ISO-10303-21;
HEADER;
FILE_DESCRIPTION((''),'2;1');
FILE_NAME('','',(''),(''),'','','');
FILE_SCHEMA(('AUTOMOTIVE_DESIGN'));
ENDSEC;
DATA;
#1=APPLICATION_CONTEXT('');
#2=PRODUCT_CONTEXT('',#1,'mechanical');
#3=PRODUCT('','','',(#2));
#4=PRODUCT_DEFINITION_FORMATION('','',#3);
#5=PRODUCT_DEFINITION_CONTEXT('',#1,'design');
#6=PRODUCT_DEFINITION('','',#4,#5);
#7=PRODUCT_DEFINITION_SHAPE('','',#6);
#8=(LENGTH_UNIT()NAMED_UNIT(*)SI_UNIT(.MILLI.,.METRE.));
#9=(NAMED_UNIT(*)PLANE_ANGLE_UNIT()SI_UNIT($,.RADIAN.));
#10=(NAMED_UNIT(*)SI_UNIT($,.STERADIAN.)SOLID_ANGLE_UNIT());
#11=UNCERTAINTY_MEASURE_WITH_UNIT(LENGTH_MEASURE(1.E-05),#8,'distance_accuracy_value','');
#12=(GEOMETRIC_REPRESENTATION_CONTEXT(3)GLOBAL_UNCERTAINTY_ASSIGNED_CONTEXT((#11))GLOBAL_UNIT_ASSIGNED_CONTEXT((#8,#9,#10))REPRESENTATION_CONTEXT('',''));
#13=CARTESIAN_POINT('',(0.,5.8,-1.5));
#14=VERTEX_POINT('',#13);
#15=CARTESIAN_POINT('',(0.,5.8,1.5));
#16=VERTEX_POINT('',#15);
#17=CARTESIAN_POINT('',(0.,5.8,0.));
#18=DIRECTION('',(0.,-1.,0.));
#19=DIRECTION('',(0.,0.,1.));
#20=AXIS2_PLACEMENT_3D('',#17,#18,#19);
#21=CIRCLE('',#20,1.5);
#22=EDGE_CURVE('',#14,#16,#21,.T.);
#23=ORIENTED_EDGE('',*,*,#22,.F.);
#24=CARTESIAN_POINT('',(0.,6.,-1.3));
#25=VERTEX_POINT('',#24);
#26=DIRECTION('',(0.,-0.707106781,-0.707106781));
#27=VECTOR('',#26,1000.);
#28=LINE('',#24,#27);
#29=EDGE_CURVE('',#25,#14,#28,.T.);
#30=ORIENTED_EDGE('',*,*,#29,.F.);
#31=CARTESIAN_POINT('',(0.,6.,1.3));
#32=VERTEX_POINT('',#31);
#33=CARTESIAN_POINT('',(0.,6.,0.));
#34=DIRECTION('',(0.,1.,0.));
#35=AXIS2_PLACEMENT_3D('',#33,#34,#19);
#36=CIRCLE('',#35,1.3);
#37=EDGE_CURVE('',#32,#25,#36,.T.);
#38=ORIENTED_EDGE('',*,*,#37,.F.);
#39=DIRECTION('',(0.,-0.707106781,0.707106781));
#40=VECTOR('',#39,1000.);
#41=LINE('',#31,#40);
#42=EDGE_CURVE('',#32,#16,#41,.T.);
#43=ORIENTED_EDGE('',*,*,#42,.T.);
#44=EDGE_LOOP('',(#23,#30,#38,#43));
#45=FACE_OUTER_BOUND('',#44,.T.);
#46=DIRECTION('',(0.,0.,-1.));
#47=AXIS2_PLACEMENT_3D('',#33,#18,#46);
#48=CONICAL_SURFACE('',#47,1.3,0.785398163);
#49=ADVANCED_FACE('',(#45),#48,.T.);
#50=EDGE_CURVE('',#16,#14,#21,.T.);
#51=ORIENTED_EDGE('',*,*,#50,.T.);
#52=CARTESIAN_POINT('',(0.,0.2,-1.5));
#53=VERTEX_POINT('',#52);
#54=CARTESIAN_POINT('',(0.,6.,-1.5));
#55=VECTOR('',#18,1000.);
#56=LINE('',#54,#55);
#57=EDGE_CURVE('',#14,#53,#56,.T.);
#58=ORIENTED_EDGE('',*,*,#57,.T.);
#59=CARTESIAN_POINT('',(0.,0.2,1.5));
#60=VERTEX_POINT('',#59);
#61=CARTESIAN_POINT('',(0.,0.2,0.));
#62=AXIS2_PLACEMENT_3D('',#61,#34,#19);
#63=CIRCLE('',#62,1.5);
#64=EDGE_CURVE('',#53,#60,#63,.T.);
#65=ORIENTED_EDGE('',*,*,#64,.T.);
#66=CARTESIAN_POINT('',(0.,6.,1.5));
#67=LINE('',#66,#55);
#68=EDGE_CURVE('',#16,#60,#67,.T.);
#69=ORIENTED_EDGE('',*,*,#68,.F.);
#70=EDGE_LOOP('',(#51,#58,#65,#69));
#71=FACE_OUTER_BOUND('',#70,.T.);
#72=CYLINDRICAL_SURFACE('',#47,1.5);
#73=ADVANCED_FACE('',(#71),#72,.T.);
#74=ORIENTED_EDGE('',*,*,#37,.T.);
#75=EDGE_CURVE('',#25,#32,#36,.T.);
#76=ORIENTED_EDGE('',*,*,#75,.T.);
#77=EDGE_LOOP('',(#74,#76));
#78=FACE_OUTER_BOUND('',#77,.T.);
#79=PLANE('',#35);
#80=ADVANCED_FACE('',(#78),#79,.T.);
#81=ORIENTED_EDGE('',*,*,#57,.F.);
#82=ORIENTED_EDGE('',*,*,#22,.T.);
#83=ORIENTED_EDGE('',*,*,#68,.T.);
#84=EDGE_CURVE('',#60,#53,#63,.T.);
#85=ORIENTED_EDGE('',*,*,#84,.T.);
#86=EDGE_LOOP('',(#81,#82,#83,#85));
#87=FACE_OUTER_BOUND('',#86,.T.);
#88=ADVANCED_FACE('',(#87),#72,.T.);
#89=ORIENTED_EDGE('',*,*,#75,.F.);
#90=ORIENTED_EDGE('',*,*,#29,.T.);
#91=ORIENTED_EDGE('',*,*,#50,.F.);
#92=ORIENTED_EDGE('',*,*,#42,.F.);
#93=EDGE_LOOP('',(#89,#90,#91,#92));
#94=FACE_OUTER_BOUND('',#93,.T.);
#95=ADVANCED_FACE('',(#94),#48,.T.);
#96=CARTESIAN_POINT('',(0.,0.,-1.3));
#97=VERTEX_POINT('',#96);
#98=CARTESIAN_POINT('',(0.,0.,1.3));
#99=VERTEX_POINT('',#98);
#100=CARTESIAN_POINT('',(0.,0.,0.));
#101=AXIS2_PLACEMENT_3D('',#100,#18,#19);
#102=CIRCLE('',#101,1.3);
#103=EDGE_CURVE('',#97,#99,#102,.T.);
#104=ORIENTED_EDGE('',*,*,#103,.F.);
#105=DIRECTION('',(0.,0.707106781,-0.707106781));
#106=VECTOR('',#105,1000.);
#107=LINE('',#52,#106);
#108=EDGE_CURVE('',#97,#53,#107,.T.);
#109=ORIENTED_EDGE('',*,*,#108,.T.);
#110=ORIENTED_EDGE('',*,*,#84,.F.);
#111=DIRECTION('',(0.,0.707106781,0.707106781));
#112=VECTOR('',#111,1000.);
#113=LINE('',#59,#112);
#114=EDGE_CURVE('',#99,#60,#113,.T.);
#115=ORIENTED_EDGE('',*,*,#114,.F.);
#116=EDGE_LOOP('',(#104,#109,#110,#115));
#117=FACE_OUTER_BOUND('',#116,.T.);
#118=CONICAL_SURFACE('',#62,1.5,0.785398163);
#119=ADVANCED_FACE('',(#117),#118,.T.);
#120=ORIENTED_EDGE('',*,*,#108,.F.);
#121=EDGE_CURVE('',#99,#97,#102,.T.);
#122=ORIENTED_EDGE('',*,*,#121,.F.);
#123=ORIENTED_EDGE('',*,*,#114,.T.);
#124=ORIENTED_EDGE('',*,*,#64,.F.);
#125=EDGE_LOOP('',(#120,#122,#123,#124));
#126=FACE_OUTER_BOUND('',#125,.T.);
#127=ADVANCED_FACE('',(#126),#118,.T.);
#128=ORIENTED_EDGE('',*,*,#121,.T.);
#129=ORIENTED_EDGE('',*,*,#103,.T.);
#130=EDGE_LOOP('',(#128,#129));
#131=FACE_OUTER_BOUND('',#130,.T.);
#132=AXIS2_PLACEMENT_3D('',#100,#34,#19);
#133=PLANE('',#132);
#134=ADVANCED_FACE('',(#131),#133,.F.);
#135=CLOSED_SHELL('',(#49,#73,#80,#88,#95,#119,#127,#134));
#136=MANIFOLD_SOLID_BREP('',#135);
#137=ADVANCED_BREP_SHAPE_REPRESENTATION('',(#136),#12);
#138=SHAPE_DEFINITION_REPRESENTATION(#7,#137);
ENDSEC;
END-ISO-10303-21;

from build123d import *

# Parameters (mm, degrees)
SKETCH1_R           = 1.5
BOSS_EXTRUDE1_DEPTH = 6
CHAMFER1_SIZE       = 0.2


with BuildPart() as part:
    # Sketch1 → Boss-Extrude1 (new body)
    with BuildSketch(Plane(origin=(0, 0, 0), x_dir=(1, 0, 0), z_dir=(0, 1, 0))):
        with Locations(Location((0, 0, 0), (0, 0, 270))):
            Circle(SKETCH1_R)
    extrude(amount=BOSS_EXTRUDE1_DEPTH)

    # Chamfer1
    chamfer1_edges = [part.edges().sort_by_distance(p)[0] for p in [
        (0, 0, -1.5),
        (0, 6, -1.5),
    ]]
    chamfer(chamfer1_edges, length=CHAMFER1_SIZE)


solid = part.part
